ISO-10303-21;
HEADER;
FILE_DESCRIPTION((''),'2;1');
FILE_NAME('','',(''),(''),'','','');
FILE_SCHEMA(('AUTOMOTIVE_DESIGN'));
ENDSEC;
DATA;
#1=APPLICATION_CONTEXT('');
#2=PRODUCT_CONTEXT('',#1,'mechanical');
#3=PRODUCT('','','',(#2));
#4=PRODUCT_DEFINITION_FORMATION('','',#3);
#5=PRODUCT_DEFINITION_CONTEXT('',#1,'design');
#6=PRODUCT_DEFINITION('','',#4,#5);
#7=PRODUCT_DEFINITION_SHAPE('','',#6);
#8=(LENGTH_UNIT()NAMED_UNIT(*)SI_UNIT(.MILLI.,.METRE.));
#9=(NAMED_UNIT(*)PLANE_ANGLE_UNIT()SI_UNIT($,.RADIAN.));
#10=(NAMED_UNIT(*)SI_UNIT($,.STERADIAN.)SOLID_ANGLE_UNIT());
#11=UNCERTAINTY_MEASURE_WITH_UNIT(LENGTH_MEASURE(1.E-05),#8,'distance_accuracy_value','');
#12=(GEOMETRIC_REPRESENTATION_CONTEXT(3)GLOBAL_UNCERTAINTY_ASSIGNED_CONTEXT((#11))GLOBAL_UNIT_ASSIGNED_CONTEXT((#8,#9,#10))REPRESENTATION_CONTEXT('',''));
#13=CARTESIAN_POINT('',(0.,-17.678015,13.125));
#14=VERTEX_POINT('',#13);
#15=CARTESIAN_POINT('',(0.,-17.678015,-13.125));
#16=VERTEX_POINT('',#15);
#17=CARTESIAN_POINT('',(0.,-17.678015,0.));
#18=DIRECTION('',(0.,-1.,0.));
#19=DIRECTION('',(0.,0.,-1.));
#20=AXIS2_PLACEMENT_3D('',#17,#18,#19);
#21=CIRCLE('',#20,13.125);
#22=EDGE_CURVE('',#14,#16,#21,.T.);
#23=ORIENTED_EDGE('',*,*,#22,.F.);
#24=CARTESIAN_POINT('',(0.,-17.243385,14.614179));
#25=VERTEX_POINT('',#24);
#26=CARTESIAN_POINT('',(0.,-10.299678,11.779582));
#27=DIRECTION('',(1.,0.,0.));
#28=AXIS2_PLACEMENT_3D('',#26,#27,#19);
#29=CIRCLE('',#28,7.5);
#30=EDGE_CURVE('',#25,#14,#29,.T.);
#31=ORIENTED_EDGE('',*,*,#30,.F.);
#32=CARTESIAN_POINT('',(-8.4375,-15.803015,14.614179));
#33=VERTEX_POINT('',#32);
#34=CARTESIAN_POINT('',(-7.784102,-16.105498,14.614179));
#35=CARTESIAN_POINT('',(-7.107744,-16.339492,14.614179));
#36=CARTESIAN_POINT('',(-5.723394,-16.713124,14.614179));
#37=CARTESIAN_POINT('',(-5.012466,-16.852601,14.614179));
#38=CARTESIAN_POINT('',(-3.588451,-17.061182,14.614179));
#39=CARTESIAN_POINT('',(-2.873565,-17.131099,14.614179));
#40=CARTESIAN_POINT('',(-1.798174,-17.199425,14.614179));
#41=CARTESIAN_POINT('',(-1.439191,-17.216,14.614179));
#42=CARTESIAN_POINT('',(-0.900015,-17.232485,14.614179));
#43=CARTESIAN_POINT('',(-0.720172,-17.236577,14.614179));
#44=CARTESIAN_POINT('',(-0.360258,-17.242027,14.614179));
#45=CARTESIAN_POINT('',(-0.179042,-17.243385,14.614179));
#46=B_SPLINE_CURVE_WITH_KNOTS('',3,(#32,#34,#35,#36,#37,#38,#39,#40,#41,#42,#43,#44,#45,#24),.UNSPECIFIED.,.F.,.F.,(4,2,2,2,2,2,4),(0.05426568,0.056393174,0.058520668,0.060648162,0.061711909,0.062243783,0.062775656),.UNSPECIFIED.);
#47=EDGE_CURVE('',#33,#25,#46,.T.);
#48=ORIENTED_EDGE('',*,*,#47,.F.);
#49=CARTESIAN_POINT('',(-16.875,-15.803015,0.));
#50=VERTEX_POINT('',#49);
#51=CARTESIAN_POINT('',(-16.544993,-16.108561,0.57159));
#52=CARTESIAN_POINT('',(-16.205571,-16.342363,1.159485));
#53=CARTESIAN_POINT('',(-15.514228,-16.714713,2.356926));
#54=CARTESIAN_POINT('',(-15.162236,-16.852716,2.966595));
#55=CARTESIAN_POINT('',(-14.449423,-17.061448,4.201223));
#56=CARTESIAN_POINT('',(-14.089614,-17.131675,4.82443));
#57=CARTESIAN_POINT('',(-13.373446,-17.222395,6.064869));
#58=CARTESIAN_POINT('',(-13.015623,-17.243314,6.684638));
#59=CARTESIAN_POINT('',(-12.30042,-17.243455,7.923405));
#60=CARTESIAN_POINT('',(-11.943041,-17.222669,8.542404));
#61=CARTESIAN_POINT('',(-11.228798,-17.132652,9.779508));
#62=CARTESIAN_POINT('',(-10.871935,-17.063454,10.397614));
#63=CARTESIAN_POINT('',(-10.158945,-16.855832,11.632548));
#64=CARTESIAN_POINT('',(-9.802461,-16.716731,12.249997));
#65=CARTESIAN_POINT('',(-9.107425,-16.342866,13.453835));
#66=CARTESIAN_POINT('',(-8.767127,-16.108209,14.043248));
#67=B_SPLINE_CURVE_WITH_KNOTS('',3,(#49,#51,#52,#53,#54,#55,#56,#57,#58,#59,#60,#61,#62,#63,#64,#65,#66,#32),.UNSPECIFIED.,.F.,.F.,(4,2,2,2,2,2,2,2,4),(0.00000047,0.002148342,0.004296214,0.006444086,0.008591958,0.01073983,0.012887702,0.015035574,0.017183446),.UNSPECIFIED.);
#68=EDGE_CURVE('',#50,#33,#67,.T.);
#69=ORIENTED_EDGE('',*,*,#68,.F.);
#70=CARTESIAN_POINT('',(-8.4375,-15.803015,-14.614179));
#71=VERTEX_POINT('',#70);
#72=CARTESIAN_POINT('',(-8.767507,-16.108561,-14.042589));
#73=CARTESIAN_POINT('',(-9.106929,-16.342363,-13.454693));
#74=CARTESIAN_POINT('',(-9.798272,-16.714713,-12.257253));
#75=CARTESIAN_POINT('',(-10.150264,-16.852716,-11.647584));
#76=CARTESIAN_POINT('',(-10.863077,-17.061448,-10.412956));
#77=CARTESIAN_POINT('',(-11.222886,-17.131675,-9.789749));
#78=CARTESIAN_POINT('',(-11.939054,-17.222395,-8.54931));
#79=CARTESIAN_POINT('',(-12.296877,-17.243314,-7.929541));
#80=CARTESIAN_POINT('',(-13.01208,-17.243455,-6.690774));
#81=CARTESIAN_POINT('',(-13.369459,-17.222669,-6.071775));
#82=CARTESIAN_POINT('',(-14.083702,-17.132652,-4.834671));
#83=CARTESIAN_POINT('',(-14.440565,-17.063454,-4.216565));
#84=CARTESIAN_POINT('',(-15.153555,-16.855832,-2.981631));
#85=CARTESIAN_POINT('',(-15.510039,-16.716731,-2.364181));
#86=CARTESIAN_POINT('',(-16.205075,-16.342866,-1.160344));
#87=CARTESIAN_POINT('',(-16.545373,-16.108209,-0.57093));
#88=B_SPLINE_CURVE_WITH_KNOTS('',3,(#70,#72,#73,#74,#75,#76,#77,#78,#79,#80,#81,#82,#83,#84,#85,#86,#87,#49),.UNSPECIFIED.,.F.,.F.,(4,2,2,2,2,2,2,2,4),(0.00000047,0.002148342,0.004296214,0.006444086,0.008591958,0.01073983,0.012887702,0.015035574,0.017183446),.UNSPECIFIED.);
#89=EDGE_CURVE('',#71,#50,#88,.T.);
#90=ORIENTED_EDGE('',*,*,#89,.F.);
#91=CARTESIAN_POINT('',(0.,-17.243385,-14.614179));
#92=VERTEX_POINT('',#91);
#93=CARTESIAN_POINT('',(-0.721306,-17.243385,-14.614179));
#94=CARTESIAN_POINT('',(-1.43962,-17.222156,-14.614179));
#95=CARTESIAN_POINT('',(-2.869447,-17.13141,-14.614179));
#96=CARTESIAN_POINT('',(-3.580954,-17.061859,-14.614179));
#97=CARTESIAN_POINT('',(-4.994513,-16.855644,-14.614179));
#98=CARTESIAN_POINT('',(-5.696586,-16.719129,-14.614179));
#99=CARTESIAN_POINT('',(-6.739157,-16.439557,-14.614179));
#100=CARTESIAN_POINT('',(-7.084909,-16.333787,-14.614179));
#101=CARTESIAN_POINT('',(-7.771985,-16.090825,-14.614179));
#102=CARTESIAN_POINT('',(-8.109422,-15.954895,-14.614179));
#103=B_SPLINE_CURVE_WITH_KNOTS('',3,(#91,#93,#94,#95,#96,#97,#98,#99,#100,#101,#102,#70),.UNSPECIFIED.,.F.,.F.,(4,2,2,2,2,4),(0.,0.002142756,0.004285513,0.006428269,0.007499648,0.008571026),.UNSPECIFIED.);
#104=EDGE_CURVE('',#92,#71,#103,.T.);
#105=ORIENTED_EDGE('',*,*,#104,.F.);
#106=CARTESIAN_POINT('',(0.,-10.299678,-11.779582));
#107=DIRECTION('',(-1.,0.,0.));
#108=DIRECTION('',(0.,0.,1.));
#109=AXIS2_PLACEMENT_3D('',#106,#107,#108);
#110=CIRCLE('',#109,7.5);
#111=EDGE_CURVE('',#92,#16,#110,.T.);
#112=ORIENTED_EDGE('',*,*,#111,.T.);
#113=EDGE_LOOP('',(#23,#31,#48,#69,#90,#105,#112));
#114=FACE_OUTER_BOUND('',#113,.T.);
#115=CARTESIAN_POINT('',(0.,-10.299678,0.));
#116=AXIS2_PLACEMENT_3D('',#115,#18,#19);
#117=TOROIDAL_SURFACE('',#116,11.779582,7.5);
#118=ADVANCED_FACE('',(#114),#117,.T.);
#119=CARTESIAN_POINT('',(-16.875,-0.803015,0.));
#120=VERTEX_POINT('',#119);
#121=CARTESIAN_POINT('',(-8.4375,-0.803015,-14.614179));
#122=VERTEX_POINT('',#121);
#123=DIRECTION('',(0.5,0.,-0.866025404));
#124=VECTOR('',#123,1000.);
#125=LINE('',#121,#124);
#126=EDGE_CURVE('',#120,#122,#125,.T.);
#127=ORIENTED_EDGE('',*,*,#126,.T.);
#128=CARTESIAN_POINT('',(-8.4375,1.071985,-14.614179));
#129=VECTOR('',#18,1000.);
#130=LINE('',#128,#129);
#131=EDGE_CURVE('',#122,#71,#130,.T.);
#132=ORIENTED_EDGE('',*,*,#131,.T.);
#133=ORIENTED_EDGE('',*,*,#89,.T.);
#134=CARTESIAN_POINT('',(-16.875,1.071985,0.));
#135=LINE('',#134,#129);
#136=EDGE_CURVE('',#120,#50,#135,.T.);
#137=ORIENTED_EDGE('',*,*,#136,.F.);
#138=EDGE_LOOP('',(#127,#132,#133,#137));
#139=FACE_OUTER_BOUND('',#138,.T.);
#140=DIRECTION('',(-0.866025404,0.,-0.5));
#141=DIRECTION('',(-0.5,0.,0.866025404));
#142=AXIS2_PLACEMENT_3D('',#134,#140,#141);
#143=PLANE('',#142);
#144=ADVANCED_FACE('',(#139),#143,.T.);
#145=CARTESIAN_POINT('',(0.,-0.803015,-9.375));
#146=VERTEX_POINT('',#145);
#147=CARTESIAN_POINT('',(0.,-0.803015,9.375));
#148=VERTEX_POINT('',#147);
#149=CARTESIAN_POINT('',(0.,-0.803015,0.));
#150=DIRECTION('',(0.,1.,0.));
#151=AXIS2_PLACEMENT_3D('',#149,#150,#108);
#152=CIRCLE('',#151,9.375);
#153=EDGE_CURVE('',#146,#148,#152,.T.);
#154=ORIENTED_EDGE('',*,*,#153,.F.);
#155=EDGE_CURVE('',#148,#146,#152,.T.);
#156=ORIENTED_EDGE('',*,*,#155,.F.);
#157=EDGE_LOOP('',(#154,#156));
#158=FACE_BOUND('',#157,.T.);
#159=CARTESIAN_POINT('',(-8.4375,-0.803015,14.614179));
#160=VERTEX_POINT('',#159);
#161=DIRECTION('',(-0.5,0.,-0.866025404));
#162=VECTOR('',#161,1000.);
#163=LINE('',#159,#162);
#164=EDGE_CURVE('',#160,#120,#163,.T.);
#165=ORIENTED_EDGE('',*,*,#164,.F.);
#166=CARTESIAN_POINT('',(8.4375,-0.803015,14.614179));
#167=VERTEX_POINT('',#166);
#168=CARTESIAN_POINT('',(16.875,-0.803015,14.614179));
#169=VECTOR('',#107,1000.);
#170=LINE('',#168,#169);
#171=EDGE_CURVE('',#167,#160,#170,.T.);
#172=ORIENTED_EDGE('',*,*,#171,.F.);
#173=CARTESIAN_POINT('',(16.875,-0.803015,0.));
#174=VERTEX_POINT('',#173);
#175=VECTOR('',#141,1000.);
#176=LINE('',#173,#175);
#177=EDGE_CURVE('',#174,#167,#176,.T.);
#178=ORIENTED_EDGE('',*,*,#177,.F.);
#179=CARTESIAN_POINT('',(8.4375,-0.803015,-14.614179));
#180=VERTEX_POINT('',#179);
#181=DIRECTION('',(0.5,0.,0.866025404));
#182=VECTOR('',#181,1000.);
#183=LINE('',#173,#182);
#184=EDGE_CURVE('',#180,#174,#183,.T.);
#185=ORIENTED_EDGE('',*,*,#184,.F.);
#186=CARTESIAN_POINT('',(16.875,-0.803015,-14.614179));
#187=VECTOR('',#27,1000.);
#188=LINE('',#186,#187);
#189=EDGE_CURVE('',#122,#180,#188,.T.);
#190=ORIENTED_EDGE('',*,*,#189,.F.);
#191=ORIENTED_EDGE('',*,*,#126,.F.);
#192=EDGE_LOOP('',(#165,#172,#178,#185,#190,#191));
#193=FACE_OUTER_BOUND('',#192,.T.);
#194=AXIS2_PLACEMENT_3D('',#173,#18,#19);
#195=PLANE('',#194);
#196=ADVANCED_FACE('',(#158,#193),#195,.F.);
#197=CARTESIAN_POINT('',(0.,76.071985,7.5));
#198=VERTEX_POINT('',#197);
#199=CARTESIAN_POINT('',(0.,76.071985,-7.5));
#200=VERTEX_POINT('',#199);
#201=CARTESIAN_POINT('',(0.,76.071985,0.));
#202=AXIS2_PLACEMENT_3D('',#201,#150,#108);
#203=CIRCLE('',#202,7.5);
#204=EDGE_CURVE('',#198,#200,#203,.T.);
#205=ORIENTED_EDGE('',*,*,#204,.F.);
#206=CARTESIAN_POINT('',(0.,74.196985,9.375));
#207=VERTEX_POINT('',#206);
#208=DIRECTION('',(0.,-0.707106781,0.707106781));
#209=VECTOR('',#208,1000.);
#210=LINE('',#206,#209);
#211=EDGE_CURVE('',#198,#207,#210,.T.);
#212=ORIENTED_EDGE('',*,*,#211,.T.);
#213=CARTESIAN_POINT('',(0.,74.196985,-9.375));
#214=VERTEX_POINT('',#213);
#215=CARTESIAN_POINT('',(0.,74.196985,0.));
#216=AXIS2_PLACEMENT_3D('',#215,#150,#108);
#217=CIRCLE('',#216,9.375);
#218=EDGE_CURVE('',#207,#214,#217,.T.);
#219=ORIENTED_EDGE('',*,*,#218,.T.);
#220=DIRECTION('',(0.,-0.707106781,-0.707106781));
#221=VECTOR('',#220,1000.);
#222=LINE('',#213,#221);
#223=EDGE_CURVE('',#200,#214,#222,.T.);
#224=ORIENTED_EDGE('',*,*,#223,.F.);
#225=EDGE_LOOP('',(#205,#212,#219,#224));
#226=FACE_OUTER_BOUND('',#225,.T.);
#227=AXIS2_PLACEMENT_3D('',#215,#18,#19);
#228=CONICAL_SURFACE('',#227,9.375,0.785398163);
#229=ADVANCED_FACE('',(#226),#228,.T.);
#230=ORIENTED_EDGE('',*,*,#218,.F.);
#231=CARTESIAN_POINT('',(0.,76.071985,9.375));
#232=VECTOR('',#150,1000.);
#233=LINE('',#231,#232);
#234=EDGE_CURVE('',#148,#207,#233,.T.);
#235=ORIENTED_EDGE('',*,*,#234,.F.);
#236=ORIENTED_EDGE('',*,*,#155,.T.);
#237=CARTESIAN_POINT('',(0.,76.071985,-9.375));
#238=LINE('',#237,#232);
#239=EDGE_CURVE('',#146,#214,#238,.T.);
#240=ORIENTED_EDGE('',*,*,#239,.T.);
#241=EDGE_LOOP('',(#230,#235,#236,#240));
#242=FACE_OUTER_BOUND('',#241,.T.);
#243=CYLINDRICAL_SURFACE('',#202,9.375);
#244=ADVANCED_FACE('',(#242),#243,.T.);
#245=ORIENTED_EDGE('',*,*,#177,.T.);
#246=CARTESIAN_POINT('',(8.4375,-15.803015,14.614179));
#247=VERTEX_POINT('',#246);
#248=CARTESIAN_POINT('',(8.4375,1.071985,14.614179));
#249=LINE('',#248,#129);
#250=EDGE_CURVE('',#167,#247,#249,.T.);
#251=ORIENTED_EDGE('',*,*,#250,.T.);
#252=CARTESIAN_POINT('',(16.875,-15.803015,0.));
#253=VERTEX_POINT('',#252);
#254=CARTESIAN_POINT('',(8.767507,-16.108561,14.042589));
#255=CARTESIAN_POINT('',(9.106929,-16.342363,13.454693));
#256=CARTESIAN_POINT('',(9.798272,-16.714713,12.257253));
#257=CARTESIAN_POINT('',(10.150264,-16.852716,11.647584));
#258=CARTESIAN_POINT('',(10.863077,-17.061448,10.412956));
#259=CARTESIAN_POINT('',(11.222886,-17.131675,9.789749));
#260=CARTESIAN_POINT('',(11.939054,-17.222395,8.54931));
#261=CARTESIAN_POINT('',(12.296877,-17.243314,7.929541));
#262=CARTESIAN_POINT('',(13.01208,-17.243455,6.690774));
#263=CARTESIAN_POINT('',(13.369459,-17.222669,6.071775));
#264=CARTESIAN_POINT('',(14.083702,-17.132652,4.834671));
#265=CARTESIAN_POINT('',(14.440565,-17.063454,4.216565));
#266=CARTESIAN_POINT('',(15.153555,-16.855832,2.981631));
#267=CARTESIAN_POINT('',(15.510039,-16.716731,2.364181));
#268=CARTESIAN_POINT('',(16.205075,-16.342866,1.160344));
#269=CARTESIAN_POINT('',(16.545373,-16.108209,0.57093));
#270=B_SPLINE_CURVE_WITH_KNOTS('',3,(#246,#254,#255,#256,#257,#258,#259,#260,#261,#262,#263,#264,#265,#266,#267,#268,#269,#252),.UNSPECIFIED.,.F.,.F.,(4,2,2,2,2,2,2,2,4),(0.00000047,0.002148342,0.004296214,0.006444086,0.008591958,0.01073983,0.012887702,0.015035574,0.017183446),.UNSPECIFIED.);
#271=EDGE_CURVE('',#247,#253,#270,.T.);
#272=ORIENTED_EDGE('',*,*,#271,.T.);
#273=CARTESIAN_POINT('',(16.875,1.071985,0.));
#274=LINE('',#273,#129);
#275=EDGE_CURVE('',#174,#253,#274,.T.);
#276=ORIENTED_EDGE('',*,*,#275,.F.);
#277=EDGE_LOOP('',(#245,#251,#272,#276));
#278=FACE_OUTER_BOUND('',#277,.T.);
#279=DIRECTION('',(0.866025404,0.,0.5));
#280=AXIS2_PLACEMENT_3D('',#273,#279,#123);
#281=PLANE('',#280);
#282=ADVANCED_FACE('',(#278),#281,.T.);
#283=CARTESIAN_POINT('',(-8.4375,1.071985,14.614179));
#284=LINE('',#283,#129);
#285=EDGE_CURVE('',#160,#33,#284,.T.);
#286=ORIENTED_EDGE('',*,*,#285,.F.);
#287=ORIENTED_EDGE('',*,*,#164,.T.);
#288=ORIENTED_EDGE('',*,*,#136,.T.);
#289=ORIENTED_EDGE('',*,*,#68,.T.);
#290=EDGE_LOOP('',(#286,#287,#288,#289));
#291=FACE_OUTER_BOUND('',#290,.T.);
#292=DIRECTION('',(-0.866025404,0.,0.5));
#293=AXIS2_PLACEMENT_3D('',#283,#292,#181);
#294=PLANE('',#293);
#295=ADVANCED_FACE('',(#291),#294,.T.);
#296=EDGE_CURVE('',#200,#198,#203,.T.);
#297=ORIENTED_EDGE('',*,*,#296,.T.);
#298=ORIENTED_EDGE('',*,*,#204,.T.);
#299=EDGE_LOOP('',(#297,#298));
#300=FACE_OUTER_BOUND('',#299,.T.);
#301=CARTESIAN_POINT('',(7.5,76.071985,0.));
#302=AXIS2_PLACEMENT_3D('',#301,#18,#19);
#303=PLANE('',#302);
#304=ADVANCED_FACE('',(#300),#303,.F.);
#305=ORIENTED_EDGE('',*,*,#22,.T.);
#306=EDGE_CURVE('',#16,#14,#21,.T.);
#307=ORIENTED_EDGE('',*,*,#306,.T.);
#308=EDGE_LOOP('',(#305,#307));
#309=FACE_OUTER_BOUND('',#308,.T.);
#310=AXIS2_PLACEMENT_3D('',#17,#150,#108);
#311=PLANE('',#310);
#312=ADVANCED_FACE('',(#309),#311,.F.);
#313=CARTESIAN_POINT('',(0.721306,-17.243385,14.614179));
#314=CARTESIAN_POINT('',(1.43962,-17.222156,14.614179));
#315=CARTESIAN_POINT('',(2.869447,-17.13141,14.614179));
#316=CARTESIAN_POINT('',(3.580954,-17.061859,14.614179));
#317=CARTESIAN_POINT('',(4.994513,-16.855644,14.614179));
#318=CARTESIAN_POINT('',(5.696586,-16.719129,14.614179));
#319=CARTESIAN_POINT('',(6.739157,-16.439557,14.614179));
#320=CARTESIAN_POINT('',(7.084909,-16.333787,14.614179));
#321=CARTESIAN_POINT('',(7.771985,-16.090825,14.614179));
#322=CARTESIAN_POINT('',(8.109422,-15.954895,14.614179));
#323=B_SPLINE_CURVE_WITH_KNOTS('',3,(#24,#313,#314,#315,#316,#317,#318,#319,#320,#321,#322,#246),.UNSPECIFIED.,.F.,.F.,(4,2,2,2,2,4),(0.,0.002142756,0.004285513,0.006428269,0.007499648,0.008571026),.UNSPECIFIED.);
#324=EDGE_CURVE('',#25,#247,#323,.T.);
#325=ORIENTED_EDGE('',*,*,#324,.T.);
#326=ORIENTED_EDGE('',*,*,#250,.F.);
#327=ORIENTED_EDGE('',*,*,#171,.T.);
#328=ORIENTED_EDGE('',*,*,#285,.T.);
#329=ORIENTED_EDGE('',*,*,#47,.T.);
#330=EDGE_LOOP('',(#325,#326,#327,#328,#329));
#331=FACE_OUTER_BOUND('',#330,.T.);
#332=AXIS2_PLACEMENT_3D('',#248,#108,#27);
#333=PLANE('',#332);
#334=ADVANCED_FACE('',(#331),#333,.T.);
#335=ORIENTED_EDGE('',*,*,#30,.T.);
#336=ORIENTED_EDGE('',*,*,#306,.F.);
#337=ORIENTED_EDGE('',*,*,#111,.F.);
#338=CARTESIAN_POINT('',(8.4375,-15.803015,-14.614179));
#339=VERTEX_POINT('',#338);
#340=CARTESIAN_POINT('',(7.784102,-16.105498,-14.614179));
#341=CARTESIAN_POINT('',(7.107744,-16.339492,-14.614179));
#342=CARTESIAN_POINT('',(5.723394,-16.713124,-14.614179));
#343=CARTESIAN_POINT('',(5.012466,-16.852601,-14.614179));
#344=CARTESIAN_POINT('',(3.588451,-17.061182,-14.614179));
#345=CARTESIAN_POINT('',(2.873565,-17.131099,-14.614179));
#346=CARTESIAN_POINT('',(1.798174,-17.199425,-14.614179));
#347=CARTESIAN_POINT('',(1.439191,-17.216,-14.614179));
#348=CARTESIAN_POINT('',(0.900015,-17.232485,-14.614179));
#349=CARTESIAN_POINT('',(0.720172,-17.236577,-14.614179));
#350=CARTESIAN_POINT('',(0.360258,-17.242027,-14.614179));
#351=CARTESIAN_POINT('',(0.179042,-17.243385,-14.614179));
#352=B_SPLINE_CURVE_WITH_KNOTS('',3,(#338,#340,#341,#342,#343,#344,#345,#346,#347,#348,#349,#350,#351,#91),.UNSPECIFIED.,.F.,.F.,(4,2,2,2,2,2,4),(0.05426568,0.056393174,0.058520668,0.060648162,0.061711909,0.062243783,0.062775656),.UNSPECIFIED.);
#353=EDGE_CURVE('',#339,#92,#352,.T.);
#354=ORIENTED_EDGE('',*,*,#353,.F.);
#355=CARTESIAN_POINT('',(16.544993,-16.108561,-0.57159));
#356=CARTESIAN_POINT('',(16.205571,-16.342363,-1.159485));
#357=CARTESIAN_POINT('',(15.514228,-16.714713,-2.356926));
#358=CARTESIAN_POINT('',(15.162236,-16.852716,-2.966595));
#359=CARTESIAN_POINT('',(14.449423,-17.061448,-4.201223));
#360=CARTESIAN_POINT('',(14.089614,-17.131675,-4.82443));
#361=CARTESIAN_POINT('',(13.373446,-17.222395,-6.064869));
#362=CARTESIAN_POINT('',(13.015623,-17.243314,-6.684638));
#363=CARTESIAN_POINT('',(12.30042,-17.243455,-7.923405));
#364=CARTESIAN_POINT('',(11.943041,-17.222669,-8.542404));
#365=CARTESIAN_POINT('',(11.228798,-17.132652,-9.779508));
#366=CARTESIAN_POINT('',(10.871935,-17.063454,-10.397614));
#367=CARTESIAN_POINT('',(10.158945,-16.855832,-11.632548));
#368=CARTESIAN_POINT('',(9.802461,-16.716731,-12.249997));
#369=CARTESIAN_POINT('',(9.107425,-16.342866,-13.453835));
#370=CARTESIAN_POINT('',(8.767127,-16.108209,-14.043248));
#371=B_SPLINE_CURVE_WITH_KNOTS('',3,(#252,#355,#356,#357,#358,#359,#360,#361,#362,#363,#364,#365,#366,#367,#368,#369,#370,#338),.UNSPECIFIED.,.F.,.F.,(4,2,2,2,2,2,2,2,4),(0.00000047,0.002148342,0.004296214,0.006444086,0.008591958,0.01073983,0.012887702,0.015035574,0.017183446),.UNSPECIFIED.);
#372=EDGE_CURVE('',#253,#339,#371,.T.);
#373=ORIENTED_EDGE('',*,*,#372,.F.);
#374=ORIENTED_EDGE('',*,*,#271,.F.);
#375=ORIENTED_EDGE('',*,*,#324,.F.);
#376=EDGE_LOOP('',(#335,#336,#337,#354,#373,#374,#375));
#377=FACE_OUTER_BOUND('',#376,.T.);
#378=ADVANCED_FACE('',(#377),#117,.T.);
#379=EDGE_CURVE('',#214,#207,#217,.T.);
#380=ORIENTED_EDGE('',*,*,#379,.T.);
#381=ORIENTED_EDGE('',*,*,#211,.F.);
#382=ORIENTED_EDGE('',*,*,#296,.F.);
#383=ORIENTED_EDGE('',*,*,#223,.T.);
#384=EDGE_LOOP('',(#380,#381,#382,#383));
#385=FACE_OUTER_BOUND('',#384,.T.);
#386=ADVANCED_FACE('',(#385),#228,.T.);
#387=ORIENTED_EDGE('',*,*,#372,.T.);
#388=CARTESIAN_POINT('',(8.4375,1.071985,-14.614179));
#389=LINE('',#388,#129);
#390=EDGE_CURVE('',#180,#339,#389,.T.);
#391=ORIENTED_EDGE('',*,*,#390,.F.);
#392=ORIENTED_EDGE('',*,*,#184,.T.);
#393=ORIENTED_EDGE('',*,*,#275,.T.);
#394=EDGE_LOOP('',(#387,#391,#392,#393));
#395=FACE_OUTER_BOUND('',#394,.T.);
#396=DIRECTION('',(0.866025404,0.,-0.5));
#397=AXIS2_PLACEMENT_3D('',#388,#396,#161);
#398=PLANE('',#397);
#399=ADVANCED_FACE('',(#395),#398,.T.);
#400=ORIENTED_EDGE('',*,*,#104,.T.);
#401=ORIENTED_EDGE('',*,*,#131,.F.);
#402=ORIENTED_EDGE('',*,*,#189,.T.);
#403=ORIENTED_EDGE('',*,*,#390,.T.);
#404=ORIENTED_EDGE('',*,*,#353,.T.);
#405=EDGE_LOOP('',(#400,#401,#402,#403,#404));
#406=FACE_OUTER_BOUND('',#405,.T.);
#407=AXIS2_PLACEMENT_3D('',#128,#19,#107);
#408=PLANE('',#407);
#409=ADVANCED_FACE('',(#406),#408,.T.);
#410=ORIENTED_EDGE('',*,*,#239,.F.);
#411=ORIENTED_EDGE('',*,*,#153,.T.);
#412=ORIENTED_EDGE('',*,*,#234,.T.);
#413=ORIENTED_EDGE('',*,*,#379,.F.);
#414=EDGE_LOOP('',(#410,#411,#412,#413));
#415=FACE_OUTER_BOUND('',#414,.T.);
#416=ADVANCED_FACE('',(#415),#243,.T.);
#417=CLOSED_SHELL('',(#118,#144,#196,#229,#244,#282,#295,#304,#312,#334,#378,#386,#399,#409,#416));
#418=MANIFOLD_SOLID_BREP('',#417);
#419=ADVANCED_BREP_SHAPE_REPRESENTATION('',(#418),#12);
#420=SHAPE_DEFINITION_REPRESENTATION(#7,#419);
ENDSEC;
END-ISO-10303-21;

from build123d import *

# Parameters (mm, degrees)
SKETCH2_OUTSIDE_W  = 31.222
SKETCH2_OUTSIDE_H  = 31.222
CUT_EXTRUDE2_DEPTH = 10
SCALE_1_SCALE      = 1.875


with BuildPart() as part:
    # Sketch1 → Revolve1 (revolve)
    with BuildSketch(Plane.XY, mode=Mode.PRIVATE) as revolve1_sk:
        Polygon((0, 0), (9, 0), (9, 9), (5, 9), (5, 49), (4, 50), (0, 50), align=None)
    revolve(revolve1_sk.sketch.rotate(Axis((0, 50, 0), (0, -1, 0)), 90), axis=Axis((0, 50, 0), (0, -1, 0)))

    # Sketch2 outside → Cut-Extrude2 (cut)
    with BuildSketch(Plane.XZ):
        Rectangle(SKETCH2_OUTSIDE_W, SKETCH2_OUTSIDE_H)
        Polygon((9, 0), (4.5, 7.794228634), (-4.5, 7.794228634), (-9, 0), (-4.5, -7.794228634), (4.5, -7.794228634), align=None, mode=Mode.SUBTRACT)
    extrude(amount=-CUT_EXTRUDE2_DEPTH, mode=Mode.SUBTRACT)

    # Sketch5 → Cut-Revolve2 (revolve, cut)
    with BuildSketch(Plane.XY, mode=Mode.PRIVATE) as cut_revolve2_sk:
        with BuildLine():
            Line((-9, 0), (-9, 1))
            ThreePointArc((-9, 1), (-8.071297978, 0.357404043), (-7, 0))
            Line((-7, 0), (-9, 0))
        make_face()
    revolve(cut_revolve2_sk.sketch.rotate(Axis((0, 0, 0), (0, 1, 0)), 270), axis=Axis((0, 0, 0), (0, 1, 0)), mode=Mode.SUBTRACT)


with BuildPart() as part_1:
    # Scale 1: scaled about (-2.65e-07, 20.203740947, 0)
    add(part.part.scale(SCALE_1_SCALE).moved(Location((2.32e-07, -17.678273329, 0))))


solid = part_1.part
